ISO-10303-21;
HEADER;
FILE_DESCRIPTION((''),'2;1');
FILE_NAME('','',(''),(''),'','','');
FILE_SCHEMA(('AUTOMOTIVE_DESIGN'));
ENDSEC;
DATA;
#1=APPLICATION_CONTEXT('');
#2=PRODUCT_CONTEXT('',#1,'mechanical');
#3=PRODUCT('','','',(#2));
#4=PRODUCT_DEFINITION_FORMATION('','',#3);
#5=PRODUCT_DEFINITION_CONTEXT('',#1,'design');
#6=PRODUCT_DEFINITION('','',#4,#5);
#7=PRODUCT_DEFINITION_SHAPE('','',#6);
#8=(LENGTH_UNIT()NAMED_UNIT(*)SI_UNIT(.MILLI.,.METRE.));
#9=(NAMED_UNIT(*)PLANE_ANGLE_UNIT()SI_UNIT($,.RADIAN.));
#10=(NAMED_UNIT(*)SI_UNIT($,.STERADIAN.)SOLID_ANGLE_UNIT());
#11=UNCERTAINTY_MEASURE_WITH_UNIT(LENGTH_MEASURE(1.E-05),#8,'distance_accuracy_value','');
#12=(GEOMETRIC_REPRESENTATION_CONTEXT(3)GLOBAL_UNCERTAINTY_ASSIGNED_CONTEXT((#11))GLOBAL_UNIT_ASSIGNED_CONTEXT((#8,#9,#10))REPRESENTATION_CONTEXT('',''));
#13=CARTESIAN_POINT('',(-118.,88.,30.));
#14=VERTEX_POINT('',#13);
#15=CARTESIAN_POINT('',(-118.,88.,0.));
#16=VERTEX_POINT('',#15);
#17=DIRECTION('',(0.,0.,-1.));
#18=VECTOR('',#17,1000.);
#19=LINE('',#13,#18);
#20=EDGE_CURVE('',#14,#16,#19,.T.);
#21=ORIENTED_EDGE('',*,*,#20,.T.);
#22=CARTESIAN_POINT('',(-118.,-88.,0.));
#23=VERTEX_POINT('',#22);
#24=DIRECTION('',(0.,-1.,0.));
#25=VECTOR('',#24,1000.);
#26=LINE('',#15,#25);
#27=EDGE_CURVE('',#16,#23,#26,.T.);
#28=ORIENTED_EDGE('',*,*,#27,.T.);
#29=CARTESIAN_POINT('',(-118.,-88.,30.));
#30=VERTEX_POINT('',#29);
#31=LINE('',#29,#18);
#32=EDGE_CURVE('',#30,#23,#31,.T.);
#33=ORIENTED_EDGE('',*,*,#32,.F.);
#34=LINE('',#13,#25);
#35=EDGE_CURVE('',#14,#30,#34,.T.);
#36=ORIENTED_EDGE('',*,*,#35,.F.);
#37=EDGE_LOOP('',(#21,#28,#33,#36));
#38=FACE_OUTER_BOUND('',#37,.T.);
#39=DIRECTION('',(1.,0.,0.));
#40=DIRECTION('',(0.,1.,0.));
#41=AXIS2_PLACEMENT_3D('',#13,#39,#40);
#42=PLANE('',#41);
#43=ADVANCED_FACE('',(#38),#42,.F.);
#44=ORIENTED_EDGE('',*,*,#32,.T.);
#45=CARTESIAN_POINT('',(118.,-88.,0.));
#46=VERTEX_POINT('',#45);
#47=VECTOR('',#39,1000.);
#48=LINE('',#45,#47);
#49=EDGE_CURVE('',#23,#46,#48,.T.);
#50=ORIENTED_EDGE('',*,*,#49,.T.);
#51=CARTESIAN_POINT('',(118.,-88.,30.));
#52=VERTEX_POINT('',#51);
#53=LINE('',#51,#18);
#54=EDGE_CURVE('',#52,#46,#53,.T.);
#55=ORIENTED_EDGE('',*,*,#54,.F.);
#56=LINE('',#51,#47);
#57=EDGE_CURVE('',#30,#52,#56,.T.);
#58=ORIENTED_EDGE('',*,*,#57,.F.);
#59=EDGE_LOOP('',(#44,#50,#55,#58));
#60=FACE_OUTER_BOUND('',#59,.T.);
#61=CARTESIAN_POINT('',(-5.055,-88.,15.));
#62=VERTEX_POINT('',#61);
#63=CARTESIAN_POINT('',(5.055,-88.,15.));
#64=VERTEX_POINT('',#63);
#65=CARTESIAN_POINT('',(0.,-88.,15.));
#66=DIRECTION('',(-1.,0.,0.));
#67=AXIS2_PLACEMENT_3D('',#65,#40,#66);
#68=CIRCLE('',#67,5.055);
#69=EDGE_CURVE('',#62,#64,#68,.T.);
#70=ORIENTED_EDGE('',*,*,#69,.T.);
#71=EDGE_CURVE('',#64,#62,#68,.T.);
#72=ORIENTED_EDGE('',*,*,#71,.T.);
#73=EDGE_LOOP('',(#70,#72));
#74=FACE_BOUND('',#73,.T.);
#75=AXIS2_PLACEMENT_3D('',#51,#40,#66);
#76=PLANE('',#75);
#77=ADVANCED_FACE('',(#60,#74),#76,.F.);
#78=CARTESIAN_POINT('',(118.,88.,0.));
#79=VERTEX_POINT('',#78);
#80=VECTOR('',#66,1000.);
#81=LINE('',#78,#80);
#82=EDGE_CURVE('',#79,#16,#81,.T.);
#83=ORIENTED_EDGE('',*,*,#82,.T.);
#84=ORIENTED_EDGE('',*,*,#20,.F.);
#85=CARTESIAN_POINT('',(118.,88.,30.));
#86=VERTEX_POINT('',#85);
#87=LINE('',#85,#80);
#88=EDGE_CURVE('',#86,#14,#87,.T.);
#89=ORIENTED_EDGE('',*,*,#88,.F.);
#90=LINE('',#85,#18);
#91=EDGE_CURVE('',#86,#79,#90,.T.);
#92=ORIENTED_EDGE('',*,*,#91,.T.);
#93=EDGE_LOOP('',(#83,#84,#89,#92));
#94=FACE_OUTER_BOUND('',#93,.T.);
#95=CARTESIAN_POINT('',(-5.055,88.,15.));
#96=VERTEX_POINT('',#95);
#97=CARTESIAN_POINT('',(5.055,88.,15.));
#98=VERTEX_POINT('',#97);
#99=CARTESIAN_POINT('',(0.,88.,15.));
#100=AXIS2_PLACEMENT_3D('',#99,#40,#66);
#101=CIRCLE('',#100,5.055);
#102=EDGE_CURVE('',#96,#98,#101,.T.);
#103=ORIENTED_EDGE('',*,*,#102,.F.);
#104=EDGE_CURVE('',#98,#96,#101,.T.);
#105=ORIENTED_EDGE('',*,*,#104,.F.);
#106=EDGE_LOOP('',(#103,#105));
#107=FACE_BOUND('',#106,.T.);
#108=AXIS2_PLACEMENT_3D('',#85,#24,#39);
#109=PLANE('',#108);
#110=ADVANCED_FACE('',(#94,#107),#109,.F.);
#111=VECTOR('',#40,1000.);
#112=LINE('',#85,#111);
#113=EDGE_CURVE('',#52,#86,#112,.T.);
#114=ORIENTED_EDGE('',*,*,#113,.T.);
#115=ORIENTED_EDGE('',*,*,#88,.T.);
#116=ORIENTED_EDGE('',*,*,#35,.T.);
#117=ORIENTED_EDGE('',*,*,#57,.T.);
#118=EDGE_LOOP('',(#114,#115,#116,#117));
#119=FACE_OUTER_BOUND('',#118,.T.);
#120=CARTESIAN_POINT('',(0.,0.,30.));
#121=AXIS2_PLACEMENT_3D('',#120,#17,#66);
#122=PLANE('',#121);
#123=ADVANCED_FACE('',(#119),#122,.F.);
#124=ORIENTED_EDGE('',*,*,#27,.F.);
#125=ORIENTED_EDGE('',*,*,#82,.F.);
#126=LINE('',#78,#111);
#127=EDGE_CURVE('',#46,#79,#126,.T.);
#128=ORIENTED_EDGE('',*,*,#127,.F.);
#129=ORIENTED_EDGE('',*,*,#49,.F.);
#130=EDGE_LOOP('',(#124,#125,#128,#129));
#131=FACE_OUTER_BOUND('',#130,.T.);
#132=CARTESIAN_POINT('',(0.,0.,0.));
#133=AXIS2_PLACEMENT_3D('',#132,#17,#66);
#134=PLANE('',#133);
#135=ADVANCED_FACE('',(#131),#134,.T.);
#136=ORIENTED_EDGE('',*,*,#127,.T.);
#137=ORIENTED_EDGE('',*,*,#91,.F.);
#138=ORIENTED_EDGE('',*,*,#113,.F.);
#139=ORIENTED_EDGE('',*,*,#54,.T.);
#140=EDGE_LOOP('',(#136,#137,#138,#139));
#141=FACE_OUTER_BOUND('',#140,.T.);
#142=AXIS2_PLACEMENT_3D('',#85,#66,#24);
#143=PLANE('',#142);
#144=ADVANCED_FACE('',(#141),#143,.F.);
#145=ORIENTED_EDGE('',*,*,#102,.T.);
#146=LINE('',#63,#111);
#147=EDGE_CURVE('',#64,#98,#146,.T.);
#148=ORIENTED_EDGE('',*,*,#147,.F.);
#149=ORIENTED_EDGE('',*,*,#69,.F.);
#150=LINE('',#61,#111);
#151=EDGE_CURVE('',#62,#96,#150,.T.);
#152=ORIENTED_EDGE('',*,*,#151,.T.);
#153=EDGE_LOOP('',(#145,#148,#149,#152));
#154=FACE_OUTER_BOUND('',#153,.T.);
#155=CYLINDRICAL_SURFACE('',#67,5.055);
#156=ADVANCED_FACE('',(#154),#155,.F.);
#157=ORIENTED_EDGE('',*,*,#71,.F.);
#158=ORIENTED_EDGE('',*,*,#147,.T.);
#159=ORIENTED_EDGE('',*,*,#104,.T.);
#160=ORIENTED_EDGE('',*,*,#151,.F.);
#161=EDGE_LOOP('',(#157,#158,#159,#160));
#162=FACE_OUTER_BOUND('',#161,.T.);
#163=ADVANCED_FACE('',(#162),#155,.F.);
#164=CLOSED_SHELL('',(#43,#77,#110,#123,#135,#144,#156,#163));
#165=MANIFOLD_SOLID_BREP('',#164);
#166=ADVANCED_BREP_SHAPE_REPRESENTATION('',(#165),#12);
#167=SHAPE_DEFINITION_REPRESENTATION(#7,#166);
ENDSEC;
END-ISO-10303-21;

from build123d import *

# Parameters (mm, degrees)
SKETCH1_W           = 236
SKETCH1_H           = 176
BOSS_EXTRUDE1_DEPTH = 30
SKETCH3_R           = 5.055
CUT_EXTRUDE1_DEPTH  = 215.00934559


with BuildPart() as part:
    # Sketch1 → Boss-Extrude1 (new body)
    with BuildSketch(Plane.XY):
        Rectangle(SKETCH1_W, SKETCH1_H)
    extrude(amount=BOSS_EXTRUDE1_DEPTH)

    # Sketch3 → Cut-Extrude1 (cut, through all)
    with BuildSketch(Plane(origin=(0, 88, 0), x_dir=(1, 0, 0), z_dir=(0, 1, 0))):
        with Locations(Location((0, -15, 0), (0, 0, 180))):
            Circle(SKETCH3_R)
    extrude(amount=-CUT_EXTRUDE1_DEPTH, mode=Mode.SUBTRACT)


solid = part.part
